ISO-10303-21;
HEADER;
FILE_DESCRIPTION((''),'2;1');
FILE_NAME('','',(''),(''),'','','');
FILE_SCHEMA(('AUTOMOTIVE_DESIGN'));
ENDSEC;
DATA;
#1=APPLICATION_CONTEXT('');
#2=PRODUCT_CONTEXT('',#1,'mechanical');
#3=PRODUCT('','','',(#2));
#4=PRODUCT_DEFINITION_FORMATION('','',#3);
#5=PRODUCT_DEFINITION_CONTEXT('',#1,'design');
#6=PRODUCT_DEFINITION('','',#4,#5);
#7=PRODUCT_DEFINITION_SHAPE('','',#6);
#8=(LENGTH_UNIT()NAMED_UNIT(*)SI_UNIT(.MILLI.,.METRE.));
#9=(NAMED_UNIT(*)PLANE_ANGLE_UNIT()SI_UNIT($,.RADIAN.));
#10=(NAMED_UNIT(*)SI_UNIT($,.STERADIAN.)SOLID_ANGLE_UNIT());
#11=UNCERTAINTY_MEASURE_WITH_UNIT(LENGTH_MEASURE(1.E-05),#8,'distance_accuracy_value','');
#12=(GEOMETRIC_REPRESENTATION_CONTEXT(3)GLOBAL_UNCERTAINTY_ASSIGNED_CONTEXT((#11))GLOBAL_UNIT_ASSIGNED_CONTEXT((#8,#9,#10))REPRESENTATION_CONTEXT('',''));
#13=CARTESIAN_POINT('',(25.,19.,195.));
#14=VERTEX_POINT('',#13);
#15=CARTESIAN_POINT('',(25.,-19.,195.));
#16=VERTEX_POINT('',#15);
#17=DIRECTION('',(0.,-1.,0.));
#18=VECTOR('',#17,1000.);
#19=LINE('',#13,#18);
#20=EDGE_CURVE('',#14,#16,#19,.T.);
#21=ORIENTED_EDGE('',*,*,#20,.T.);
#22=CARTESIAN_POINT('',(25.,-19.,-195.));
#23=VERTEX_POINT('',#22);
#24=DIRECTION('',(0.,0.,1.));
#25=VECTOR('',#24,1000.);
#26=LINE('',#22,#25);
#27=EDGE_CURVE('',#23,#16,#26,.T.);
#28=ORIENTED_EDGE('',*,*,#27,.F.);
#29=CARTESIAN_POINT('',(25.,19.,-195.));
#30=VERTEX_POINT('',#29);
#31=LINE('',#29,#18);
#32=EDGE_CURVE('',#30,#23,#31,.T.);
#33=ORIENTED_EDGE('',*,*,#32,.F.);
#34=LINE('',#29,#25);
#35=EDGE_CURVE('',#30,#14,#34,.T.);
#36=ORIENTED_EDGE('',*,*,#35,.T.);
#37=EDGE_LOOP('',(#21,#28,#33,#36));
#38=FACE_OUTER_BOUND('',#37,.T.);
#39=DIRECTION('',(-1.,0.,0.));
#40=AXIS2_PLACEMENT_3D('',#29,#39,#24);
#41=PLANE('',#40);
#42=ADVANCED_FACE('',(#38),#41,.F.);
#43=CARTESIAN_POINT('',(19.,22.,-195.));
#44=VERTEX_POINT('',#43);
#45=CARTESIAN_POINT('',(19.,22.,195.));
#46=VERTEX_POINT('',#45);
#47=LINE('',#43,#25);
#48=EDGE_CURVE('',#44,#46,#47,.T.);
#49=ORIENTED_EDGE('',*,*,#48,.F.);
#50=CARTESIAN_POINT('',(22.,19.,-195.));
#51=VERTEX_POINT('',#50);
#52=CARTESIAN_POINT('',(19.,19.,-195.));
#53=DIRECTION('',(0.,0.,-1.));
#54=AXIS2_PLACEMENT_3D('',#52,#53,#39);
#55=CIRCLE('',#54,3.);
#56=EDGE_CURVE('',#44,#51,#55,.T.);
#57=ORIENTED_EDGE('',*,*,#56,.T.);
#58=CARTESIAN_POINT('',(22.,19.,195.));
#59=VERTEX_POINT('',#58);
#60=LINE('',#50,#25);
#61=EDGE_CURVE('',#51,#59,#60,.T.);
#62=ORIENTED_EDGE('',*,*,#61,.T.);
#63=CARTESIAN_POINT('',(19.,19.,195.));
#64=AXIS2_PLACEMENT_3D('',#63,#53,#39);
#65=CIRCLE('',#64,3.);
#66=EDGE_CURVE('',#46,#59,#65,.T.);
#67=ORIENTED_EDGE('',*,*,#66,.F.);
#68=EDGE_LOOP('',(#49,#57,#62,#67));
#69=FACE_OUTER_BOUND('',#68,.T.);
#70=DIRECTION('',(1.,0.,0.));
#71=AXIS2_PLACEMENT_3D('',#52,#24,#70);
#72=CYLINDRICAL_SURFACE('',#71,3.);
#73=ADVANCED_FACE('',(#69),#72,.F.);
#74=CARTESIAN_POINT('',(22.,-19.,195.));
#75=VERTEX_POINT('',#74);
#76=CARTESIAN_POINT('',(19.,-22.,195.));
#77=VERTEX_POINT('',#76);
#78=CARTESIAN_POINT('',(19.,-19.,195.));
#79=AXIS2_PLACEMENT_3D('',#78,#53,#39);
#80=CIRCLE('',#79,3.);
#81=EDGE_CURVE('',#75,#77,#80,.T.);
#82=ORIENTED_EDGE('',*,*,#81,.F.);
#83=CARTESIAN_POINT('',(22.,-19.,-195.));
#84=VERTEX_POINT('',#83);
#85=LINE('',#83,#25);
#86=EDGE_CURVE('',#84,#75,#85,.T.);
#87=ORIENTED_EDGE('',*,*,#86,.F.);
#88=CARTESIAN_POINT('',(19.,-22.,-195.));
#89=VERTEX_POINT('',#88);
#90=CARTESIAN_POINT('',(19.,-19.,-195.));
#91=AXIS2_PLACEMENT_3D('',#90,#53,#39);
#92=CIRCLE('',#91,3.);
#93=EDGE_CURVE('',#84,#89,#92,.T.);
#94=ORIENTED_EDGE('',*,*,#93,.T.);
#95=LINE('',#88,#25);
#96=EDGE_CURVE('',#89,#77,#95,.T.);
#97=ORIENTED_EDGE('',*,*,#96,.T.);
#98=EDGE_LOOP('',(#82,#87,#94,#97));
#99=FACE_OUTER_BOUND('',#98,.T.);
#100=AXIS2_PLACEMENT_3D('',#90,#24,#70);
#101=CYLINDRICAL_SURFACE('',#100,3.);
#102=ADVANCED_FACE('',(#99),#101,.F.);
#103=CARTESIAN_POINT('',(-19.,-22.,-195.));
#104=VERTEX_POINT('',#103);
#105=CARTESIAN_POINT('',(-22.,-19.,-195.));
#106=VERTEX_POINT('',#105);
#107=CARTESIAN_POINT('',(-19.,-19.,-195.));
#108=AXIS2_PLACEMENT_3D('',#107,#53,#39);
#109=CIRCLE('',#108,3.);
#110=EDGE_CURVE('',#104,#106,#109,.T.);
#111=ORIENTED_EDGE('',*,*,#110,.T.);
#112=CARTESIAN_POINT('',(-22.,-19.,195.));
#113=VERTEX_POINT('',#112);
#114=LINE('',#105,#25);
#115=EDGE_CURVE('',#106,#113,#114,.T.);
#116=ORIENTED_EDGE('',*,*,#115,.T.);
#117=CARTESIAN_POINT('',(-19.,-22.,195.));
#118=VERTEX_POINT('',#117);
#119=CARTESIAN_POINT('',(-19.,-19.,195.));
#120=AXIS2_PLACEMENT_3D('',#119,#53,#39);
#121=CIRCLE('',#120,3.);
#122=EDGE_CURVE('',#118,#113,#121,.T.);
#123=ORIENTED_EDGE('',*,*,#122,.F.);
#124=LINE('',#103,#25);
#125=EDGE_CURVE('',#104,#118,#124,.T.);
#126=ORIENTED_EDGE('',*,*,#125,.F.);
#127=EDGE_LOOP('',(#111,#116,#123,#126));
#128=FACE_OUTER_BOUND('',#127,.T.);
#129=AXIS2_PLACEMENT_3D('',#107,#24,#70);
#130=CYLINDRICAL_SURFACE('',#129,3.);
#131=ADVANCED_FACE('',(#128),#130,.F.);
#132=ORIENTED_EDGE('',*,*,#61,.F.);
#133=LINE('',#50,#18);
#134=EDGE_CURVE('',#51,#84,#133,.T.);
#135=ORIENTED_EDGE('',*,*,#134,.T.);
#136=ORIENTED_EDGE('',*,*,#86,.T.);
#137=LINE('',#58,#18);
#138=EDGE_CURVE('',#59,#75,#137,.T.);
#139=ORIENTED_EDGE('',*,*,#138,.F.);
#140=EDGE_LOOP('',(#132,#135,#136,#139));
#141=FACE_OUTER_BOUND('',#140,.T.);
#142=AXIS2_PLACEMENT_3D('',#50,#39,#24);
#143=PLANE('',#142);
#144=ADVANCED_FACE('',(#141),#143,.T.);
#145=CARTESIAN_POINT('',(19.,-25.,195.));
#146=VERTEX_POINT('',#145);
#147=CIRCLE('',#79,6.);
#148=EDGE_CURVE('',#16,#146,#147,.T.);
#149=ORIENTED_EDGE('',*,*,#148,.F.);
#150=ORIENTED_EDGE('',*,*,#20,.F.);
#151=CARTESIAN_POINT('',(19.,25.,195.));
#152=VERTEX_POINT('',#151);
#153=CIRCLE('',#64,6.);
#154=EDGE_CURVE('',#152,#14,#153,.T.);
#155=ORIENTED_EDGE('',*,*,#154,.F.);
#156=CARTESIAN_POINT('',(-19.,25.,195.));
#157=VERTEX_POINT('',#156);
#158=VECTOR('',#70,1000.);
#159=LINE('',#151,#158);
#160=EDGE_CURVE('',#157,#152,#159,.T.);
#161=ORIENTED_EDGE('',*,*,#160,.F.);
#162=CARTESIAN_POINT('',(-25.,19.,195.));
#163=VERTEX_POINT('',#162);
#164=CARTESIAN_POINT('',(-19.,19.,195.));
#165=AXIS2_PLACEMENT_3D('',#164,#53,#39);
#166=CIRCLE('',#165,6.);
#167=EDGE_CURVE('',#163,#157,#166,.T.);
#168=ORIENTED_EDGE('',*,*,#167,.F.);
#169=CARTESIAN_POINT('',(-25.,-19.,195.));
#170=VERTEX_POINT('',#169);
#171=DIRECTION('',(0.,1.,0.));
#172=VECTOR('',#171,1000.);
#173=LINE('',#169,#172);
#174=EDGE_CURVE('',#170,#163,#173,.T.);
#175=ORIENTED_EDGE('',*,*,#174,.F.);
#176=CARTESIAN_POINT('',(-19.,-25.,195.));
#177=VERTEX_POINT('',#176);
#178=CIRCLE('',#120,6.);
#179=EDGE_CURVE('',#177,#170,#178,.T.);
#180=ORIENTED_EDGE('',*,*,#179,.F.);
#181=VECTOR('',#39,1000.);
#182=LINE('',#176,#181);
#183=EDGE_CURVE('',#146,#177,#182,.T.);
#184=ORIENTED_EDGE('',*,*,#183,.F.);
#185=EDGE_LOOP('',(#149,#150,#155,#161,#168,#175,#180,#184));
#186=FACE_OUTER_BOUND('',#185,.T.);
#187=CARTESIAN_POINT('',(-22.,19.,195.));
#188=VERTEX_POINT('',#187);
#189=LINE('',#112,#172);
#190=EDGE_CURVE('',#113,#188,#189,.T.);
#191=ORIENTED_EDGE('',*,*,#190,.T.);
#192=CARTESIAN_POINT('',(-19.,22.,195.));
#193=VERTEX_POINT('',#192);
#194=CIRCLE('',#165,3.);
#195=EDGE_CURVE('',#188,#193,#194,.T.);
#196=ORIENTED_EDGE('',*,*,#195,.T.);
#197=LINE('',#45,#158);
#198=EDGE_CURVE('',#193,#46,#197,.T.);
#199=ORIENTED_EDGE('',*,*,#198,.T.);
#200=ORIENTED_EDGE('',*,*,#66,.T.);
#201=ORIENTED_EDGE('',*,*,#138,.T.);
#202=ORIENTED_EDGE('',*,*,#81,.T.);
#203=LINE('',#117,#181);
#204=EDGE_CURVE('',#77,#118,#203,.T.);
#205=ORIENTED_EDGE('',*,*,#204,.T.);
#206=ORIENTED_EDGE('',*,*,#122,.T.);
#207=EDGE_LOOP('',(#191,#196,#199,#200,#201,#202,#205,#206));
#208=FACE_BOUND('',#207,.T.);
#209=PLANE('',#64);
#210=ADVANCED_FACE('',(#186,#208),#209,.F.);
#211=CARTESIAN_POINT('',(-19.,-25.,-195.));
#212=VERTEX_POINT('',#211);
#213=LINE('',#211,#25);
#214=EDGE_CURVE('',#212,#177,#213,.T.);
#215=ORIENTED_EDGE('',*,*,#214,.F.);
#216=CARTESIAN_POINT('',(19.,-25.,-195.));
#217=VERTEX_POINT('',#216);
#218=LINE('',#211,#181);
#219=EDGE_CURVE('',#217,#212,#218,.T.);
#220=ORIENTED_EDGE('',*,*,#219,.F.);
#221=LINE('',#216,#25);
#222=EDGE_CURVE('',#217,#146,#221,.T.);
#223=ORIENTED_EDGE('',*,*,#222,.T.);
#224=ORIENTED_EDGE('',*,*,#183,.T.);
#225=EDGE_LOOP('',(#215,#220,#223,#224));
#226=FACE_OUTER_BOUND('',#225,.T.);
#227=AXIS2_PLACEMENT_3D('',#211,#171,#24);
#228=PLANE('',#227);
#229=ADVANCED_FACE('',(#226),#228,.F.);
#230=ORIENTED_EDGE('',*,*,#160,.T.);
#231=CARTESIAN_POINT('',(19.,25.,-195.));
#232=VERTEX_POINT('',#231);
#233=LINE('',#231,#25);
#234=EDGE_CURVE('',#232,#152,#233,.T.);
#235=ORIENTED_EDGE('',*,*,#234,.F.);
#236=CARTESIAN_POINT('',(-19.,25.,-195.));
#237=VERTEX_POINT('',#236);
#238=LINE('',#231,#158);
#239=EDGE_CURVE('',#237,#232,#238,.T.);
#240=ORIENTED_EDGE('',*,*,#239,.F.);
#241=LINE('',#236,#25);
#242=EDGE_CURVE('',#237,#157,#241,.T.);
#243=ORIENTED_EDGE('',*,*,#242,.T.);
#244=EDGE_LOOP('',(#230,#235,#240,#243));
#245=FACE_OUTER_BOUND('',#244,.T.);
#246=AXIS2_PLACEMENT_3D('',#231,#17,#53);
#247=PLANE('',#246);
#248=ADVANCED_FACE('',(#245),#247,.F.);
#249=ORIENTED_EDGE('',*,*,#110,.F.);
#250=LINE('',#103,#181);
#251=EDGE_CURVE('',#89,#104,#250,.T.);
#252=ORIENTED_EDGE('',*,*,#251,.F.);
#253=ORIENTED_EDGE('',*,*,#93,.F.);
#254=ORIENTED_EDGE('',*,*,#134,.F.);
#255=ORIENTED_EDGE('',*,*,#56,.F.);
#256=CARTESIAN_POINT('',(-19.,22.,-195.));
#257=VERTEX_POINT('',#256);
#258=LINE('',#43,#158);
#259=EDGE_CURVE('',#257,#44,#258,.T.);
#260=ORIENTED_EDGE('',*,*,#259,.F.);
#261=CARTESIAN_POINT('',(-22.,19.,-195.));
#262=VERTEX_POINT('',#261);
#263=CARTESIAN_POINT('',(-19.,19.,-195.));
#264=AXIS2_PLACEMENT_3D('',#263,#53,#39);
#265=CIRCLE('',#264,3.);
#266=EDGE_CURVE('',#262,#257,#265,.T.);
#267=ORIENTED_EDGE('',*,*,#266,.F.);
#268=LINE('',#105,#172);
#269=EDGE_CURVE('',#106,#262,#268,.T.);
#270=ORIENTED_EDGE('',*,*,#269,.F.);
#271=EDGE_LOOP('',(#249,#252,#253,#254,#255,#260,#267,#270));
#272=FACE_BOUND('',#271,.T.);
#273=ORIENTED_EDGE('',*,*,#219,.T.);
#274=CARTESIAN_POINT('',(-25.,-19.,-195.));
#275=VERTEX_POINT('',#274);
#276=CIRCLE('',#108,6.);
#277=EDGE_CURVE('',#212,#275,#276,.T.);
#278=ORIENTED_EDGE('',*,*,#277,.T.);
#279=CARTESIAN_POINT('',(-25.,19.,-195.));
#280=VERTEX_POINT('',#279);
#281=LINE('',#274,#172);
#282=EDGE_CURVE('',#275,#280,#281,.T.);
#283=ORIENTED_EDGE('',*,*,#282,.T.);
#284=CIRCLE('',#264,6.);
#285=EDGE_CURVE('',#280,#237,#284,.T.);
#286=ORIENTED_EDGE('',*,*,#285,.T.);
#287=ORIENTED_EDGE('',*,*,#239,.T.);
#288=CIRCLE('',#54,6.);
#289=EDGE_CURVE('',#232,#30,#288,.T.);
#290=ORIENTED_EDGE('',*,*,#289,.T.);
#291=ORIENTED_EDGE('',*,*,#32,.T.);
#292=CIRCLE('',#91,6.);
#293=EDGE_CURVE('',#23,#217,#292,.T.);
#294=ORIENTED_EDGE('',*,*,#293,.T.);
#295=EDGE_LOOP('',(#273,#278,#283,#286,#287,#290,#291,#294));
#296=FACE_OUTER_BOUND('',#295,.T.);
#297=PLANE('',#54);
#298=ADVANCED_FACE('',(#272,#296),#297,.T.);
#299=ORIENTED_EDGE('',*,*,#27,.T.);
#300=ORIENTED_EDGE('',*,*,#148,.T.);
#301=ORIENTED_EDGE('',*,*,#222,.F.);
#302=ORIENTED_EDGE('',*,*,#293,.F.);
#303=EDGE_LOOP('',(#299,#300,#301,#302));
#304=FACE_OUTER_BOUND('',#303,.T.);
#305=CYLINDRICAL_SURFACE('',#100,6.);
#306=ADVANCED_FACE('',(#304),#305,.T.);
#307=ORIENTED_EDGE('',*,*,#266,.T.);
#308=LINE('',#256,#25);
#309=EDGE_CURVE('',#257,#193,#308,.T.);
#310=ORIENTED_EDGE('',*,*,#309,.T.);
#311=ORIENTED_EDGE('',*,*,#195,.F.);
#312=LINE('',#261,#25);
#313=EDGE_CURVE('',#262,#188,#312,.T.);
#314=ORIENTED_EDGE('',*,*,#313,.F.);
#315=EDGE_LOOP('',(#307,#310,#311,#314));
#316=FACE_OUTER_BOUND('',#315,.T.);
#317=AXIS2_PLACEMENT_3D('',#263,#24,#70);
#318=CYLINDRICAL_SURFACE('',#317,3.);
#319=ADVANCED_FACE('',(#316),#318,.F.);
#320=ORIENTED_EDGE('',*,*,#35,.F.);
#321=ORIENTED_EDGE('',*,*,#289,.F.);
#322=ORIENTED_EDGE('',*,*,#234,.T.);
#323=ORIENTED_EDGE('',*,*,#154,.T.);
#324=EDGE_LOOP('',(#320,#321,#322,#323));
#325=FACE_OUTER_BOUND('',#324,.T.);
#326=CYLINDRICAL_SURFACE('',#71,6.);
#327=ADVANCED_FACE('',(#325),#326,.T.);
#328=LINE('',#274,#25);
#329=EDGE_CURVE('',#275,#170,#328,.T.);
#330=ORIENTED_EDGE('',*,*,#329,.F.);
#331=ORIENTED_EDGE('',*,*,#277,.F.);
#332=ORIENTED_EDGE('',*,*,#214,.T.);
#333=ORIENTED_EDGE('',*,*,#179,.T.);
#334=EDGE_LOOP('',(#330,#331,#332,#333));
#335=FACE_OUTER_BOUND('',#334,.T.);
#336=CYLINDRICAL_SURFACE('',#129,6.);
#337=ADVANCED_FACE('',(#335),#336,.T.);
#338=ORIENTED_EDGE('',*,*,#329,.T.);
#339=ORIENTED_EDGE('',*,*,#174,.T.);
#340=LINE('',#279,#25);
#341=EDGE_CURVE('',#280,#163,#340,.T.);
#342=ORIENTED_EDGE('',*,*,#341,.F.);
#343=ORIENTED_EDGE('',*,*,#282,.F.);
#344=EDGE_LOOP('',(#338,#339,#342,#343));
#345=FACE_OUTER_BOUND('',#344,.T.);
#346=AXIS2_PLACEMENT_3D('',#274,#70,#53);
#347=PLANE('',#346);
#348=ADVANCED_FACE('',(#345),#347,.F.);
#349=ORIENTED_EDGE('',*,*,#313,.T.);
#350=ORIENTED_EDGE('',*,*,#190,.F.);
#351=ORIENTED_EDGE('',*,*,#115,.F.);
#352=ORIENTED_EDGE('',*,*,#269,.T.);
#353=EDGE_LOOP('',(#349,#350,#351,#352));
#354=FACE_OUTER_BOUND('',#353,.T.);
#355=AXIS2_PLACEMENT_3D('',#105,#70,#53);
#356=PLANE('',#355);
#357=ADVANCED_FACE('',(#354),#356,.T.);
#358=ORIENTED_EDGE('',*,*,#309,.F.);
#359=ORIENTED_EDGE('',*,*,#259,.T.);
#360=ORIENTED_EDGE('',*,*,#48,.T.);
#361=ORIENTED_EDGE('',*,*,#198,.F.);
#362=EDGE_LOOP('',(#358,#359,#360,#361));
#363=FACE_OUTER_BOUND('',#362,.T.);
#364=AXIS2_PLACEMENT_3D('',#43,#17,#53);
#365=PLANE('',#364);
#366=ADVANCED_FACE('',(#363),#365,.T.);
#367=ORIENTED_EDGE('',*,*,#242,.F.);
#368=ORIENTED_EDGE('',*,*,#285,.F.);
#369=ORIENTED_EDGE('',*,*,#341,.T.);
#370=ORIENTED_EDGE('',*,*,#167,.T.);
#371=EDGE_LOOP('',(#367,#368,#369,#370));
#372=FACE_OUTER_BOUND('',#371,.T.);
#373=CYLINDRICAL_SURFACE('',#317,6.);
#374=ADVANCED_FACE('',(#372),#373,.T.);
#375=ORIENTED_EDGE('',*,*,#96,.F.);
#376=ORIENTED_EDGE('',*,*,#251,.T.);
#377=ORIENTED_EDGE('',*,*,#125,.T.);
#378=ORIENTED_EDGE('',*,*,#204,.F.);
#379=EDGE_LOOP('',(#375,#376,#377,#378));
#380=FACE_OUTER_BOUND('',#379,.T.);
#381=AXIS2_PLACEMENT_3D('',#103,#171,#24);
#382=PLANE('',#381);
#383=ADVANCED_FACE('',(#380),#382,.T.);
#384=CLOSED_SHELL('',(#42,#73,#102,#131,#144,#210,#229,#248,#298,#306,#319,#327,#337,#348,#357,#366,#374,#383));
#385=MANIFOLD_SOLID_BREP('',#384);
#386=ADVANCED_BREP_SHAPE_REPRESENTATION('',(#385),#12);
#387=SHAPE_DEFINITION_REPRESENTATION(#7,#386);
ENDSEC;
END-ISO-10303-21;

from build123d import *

# Parameters (mm, degrees)
GB_6728_1986_050_X_50_X_3_1_DEPTH = 390


with BuildPart() as part:
    # Sketch1 → Gb／6728-1986方形空心型钢 050 X 50 X 3(1) (new body)
    with BuildSketch(Plane.YX.offset(-195)):
        with BuildLine():
            Line((-19, -25), (19, -25))
            ThreePointArc((19, -25), (23.242640687, -23.242640687), (25, -19))
            Line((25, -19), (25, 19))
            ThreePointArc((25, 19), (23.242640687, 23.242640687), (19, 25))
            Line((19, 25), (-19, 25))
            ThreePointArc((-19, 25), (-23.242640687, 23.242640687), (-25, 19))
            Line((-25, 19), (-25, -19))
            ThreePointArc((-25, -19), (-23.242640687, -23.242640687), (-19, -25))
        make_face()
        with BuildLine():
            Line((-19, -22), (19, -22))
            ThreePointArc((19, -22), (21.121320344, -21.121320344), (22, -19))
            Line((22, -19), (22, 19))
            ThreePointArc((22, 19), (21.121320344, 21.121320344), (19, 22))
            Line((19, 22), (-19, 22))
            ThreePointArc((-19, 22), (-21.121320344, 21.121320344), (-22, 19))
            Line((-22, 19), (-22, -19))
            ThreePointArc((-22, -19), (-21.121320344, -21.121320344), (-19, -22))
        make_face(mode=Mode.SUBTRACT)
    extrude(amount=GB_6728_1986_050_X_50_X_3_1_DEPTH)


solid = part.part
